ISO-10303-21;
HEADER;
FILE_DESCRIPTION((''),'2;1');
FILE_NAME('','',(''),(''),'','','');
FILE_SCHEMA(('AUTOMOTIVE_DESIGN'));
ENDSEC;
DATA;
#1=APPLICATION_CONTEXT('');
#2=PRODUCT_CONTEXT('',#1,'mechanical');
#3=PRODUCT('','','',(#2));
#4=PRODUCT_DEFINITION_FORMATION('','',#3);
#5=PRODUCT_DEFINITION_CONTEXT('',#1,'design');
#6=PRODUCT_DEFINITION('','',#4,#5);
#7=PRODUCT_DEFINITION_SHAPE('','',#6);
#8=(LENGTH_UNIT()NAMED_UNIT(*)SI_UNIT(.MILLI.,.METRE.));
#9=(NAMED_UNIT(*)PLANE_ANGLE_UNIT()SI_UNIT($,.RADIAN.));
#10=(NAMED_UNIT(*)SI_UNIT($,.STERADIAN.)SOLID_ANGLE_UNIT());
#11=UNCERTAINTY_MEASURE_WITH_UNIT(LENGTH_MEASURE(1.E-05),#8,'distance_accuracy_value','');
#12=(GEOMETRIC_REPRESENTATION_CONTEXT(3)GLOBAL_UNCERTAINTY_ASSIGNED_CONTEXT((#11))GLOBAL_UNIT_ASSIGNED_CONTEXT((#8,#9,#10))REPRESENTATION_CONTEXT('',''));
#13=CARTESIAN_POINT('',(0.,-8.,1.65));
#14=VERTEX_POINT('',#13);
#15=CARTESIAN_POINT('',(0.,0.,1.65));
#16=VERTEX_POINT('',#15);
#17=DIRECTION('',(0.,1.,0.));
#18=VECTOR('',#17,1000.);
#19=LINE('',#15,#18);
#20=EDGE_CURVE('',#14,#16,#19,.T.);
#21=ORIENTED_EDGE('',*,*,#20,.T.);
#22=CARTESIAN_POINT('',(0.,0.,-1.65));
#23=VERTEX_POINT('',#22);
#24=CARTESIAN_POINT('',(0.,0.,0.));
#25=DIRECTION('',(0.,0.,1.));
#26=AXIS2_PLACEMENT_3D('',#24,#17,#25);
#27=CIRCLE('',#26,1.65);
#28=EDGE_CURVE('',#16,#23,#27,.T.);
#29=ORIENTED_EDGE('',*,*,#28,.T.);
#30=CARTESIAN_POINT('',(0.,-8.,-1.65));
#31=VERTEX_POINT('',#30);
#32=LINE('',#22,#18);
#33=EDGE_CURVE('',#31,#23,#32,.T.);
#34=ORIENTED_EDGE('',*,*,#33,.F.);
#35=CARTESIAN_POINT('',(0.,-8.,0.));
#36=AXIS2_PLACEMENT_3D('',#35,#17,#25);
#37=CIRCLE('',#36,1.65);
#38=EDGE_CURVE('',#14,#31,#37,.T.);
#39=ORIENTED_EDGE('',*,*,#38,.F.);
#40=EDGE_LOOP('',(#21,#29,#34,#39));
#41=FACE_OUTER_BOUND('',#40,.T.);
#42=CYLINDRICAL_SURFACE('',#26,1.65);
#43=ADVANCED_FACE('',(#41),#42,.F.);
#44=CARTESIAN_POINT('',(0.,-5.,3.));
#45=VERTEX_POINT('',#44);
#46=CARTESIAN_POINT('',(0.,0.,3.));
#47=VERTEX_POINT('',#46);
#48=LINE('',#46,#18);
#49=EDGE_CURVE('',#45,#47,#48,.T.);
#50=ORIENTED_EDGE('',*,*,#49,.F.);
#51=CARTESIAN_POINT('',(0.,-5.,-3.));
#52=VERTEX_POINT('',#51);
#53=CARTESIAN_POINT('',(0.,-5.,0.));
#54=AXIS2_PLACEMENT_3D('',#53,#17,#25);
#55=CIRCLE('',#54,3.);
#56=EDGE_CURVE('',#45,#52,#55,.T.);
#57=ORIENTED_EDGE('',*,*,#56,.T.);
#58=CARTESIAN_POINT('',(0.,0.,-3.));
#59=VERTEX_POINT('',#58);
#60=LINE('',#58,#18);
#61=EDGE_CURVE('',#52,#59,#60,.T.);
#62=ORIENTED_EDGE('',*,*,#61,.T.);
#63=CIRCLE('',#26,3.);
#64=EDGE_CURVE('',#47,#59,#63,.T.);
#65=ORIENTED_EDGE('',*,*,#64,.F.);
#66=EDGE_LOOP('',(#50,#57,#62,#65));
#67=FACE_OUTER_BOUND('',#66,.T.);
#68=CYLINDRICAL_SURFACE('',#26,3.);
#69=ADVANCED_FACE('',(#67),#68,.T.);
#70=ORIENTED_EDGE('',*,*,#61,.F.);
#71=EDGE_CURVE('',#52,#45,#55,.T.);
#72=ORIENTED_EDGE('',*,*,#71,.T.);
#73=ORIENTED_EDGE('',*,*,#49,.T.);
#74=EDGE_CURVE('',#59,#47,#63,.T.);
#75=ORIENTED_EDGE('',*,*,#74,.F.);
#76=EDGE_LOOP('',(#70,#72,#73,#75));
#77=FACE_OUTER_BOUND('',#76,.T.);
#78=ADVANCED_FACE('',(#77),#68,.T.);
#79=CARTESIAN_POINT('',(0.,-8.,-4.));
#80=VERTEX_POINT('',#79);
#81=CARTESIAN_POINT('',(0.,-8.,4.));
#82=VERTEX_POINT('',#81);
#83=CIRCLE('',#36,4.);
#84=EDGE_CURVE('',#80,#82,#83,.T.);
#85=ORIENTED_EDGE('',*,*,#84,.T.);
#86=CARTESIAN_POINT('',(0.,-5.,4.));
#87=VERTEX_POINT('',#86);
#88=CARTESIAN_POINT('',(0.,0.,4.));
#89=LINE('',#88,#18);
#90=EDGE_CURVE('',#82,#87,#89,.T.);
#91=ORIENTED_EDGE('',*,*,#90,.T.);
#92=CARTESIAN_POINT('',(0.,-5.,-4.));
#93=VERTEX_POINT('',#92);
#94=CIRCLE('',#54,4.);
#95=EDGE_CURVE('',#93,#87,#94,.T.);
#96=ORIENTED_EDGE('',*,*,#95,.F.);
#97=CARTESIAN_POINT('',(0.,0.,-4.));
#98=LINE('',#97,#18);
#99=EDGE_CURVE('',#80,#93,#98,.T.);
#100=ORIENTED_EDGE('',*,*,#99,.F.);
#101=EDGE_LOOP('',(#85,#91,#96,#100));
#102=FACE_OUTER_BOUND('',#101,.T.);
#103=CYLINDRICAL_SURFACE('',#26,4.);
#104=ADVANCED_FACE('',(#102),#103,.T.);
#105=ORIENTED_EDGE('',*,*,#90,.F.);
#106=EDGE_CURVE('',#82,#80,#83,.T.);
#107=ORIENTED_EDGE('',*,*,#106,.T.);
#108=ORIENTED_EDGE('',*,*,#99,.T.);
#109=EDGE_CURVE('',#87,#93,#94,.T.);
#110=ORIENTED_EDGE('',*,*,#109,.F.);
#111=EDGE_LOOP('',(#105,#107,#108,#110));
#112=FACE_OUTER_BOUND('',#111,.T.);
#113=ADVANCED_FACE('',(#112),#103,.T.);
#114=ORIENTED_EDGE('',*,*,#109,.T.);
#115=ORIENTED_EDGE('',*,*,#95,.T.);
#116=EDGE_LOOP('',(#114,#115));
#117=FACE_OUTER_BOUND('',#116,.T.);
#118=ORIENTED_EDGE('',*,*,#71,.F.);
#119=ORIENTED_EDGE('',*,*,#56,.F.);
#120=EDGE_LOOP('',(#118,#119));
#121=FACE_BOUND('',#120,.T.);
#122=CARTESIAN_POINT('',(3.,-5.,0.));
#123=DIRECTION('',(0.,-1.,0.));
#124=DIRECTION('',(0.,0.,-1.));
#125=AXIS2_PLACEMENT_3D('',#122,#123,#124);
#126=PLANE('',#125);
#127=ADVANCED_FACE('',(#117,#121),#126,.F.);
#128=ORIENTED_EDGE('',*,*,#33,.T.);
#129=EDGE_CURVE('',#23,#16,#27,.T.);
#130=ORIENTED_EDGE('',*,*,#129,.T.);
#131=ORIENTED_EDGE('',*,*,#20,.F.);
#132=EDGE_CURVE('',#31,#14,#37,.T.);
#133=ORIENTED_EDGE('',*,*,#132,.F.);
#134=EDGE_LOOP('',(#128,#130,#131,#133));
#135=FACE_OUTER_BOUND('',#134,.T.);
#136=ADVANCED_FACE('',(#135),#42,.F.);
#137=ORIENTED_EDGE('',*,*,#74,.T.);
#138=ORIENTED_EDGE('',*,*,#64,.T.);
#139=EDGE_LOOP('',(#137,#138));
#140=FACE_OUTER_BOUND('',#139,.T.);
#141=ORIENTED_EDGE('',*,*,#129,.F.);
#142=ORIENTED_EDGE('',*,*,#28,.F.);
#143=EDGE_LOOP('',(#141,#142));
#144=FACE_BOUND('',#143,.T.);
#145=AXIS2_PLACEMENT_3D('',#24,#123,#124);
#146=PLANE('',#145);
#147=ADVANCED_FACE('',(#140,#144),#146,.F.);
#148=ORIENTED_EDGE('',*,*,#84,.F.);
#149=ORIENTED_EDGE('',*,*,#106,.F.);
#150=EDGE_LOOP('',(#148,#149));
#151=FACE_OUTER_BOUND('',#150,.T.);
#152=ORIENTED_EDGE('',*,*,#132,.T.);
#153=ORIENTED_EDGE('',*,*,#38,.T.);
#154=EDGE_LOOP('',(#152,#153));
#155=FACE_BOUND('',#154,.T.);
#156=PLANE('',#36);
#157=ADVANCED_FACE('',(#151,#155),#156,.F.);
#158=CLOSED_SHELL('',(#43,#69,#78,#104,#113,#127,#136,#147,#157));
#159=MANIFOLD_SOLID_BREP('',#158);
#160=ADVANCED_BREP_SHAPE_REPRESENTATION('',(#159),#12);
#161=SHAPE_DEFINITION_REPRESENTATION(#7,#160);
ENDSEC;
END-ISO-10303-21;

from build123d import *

# Parameters (mm, degrees)
M4_TAPPED_HOLE1_D = 3.3


with BuildPart() as part:
    # Sketch1 → Revolve1 (revolve)
    with BuildSketch(Plane.XY, mode=Mode.PRIVATE) as revolve1_sk:
        Polygon((3, 0), (3, -5), (4, -5), (4, -8), (0, -8), (0, 0), align=None)
    revolve(revolve1_sk.sketch.rotate(Axis((0, 0, 0), (0, -1, 0)), 90), axis=Axis((0, 0, 0), (0, -1, 0)))

    # M4 Tapped Hole1 (through all)
    with Locations(Plane.ZX):
        with Locations((0, 0)):
            Hole(M4_TAPPED_HOLE1_D / 2)


solid = part.part
